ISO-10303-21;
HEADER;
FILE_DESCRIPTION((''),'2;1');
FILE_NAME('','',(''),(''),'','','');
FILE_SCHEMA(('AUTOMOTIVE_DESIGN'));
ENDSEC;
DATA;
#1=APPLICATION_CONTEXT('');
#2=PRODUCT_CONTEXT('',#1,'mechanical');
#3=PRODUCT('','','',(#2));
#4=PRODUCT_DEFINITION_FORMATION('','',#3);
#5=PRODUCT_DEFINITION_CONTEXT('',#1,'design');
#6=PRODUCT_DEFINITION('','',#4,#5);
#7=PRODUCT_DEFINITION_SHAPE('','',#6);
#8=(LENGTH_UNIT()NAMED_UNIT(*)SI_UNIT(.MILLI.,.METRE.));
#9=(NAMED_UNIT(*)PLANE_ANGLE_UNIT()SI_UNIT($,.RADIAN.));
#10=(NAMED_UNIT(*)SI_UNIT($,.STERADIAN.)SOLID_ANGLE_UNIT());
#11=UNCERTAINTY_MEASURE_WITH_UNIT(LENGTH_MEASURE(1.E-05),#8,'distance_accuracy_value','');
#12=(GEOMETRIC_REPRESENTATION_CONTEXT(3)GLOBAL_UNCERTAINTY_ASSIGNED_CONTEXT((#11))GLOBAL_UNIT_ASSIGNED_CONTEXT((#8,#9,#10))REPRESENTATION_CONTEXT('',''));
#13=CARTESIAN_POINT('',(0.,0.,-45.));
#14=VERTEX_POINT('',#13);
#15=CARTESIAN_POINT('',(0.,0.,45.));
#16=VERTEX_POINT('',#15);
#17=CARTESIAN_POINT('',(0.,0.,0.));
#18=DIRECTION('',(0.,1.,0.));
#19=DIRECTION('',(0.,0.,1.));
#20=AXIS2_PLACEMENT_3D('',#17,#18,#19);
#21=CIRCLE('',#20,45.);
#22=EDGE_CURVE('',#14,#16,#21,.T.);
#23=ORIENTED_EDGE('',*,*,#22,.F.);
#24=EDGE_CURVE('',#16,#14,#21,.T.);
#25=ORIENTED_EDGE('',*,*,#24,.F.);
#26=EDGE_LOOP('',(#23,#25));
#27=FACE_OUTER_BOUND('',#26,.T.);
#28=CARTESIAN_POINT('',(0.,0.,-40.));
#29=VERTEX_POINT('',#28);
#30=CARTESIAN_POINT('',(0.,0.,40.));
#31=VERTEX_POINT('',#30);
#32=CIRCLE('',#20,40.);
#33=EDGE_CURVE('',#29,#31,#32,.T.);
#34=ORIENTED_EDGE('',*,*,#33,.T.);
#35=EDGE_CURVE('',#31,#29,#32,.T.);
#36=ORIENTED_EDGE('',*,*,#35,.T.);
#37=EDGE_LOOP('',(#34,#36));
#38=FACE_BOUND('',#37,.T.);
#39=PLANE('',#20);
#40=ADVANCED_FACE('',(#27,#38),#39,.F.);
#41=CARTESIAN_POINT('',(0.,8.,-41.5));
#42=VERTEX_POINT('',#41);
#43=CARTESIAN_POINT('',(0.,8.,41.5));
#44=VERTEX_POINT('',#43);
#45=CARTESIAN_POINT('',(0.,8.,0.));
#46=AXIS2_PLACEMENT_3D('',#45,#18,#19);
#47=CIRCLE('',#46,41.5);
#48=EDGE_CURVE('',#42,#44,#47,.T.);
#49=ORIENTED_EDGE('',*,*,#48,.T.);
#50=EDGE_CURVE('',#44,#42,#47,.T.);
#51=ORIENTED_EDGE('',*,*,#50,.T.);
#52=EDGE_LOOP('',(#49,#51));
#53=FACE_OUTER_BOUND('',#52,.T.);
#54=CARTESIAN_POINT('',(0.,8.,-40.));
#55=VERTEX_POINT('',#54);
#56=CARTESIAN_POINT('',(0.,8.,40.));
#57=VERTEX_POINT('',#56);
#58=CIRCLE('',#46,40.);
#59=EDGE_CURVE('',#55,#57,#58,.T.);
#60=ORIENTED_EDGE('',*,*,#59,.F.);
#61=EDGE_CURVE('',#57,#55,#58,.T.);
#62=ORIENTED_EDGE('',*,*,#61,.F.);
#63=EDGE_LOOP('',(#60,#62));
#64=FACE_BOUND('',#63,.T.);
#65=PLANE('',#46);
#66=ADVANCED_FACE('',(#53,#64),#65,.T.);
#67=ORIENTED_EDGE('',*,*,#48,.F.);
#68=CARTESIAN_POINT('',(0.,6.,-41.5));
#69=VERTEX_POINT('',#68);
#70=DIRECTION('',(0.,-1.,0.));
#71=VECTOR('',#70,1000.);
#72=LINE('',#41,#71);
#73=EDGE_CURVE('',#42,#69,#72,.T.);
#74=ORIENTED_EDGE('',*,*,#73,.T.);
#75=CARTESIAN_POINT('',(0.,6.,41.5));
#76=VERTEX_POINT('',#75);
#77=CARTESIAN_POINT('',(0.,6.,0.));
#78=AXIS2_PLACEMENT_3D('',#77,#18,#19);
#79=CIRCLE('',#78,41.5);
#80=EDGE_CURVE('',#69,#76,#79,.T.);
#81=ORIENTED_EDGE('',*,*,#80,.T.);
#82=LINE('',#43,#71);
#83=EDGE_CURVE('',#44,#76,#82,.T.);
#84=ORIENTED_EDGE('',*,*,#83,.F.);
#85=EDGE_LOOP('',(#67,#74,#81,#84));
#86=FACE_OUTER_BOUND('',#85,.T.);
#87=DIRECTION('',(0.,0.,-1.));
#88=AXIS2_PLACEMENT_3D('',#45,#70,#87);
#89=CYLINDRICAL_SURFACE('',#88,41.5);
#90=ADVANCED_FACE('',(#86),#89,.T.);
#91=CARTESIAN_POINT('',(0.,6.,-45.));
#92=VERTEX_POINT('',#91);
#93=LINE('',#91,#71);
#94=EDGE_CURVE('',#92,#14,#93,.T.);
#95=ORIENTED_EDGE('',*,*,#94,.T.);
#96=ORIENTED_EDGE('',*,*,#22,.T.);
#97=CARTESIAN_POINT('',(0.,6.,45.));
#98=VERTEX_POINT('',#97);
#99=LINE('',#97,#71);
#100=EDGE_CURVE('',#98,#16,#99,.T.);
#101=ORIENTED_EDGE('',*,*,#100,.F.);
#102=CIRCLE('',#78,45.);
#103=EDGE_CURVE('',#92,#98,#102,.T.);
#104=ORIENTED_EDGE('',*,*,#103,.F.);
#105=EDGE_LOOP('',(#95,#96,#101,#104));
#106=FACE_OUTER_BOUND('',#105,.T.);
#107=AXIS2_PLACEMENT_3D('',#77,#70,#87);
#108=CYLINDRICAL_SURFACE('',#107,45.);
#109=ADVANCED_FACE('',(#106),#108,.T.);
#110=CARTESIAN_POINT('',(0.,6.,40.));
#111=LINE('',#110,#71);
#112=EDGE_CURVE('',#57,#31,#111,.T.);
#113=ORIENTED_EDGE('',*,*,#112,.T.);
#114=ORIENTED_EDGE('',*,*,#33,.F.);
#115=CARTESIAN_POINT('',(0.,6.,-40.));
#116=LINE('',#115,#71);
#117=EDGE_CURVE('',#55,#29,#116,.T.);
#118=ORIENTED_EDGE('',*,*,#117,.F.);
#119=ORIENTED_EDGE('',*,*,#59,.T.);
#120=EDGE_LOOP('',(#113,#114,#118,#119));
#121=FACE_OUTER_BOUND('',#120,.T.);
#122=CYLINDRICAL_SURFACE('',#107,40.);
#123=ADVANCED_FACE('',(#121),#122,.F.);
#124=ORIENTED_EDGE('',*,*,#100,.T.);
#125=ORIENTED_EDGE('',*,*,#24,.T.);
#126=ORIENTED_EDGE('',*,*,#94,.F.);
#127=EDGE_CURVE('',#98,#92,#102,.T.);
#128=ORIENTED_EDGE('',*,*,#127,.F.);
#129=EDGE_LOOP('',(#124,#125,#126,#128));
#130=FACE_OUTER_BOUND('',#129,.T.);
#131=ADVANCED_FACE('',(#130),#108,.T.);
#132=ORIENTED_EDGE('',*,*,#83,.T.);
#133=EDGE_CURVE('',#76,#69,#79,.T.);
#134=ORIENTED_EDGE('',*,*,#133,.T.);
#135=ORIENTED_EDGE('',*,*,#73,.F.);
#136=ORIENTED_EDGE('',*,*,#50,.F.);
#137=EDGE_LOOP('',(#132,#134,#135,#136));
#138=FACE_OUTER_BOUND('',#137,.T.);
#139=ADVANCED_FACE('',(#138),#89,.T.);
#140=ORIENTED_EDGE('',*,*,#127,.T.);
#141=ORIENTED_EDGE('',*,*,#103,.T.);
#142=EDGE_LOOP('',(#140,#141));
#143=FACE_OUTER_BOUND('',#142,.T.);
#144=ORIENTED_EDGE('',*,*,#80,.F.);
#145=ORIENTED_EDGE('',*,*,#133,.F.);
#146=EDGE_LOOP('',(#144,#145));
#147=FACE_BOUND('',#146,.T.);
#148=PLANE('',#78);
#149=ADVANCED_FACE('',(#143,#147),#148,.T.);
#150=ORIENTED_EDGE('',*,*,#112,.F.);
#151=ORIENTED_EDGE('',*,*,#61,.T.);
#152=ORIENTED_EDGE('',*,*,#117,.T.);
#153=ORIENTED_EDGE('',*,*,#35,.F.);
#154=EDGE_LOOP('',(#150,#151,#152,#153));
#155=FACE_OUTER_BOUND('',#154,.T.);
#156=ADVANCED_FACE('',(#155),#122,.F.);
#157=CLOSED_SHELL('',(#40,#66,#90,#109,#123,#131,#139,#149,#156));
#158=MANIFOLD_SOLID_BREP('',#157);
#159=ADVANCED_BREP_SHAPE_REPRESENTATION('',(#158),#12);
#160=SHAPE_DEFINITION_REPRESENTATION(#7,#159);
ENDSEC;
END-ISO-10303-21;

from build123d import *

# Parameters (mm, degrees)
SKETCH1_R           = 45
SKETCH1_R_2         = 40
BOSS_EXTRUDE1_DEPTH = 6
SKETCH2_R           = 41.5
SKETCH2_R_2         = 40
BOSS_EXTRUDE2_DEPTH = 2


with BuildPart() as part:
    # Sketch1 → Boss-Extrude1 (new body)
    with BuildSketch(Plane(origin=(0, 0, 0), x_dir=(1, 0, 0), z_dir=(0, 1, 0))):
        with Locations(Location((0, 0, 0), (0, 0, 270))):
            Circle(SKETCH1_R)
        with Locations(Location((0, 0, 0), (0, 0, 270))):
            Circle(SKETCH1_R_2, mode=Mode.SUBTRACT)
    extrude(amount=BOSS_EXTRUDE1_DEPTH)

    # Sketch2 → Boss-Extrude2 (add)
    with BuildSketch(Plane(origin=(0, 6, 0), x_dir=(1, 0, 0), z_dir=(0, 1, 0))):
        with Locations(Location((0, 0, 0), (0, 0, 270))):
            Circle(SKETCH2_R)
        with Locations(Location((0, 0, 0), (0, 0, 270))):
            Circle(SKETCH2_R_2, mode=Mode.SUBTRACT)
    extrude(amount=BOSS_EXTRUDE2_DEPTH)


solid = part.part
